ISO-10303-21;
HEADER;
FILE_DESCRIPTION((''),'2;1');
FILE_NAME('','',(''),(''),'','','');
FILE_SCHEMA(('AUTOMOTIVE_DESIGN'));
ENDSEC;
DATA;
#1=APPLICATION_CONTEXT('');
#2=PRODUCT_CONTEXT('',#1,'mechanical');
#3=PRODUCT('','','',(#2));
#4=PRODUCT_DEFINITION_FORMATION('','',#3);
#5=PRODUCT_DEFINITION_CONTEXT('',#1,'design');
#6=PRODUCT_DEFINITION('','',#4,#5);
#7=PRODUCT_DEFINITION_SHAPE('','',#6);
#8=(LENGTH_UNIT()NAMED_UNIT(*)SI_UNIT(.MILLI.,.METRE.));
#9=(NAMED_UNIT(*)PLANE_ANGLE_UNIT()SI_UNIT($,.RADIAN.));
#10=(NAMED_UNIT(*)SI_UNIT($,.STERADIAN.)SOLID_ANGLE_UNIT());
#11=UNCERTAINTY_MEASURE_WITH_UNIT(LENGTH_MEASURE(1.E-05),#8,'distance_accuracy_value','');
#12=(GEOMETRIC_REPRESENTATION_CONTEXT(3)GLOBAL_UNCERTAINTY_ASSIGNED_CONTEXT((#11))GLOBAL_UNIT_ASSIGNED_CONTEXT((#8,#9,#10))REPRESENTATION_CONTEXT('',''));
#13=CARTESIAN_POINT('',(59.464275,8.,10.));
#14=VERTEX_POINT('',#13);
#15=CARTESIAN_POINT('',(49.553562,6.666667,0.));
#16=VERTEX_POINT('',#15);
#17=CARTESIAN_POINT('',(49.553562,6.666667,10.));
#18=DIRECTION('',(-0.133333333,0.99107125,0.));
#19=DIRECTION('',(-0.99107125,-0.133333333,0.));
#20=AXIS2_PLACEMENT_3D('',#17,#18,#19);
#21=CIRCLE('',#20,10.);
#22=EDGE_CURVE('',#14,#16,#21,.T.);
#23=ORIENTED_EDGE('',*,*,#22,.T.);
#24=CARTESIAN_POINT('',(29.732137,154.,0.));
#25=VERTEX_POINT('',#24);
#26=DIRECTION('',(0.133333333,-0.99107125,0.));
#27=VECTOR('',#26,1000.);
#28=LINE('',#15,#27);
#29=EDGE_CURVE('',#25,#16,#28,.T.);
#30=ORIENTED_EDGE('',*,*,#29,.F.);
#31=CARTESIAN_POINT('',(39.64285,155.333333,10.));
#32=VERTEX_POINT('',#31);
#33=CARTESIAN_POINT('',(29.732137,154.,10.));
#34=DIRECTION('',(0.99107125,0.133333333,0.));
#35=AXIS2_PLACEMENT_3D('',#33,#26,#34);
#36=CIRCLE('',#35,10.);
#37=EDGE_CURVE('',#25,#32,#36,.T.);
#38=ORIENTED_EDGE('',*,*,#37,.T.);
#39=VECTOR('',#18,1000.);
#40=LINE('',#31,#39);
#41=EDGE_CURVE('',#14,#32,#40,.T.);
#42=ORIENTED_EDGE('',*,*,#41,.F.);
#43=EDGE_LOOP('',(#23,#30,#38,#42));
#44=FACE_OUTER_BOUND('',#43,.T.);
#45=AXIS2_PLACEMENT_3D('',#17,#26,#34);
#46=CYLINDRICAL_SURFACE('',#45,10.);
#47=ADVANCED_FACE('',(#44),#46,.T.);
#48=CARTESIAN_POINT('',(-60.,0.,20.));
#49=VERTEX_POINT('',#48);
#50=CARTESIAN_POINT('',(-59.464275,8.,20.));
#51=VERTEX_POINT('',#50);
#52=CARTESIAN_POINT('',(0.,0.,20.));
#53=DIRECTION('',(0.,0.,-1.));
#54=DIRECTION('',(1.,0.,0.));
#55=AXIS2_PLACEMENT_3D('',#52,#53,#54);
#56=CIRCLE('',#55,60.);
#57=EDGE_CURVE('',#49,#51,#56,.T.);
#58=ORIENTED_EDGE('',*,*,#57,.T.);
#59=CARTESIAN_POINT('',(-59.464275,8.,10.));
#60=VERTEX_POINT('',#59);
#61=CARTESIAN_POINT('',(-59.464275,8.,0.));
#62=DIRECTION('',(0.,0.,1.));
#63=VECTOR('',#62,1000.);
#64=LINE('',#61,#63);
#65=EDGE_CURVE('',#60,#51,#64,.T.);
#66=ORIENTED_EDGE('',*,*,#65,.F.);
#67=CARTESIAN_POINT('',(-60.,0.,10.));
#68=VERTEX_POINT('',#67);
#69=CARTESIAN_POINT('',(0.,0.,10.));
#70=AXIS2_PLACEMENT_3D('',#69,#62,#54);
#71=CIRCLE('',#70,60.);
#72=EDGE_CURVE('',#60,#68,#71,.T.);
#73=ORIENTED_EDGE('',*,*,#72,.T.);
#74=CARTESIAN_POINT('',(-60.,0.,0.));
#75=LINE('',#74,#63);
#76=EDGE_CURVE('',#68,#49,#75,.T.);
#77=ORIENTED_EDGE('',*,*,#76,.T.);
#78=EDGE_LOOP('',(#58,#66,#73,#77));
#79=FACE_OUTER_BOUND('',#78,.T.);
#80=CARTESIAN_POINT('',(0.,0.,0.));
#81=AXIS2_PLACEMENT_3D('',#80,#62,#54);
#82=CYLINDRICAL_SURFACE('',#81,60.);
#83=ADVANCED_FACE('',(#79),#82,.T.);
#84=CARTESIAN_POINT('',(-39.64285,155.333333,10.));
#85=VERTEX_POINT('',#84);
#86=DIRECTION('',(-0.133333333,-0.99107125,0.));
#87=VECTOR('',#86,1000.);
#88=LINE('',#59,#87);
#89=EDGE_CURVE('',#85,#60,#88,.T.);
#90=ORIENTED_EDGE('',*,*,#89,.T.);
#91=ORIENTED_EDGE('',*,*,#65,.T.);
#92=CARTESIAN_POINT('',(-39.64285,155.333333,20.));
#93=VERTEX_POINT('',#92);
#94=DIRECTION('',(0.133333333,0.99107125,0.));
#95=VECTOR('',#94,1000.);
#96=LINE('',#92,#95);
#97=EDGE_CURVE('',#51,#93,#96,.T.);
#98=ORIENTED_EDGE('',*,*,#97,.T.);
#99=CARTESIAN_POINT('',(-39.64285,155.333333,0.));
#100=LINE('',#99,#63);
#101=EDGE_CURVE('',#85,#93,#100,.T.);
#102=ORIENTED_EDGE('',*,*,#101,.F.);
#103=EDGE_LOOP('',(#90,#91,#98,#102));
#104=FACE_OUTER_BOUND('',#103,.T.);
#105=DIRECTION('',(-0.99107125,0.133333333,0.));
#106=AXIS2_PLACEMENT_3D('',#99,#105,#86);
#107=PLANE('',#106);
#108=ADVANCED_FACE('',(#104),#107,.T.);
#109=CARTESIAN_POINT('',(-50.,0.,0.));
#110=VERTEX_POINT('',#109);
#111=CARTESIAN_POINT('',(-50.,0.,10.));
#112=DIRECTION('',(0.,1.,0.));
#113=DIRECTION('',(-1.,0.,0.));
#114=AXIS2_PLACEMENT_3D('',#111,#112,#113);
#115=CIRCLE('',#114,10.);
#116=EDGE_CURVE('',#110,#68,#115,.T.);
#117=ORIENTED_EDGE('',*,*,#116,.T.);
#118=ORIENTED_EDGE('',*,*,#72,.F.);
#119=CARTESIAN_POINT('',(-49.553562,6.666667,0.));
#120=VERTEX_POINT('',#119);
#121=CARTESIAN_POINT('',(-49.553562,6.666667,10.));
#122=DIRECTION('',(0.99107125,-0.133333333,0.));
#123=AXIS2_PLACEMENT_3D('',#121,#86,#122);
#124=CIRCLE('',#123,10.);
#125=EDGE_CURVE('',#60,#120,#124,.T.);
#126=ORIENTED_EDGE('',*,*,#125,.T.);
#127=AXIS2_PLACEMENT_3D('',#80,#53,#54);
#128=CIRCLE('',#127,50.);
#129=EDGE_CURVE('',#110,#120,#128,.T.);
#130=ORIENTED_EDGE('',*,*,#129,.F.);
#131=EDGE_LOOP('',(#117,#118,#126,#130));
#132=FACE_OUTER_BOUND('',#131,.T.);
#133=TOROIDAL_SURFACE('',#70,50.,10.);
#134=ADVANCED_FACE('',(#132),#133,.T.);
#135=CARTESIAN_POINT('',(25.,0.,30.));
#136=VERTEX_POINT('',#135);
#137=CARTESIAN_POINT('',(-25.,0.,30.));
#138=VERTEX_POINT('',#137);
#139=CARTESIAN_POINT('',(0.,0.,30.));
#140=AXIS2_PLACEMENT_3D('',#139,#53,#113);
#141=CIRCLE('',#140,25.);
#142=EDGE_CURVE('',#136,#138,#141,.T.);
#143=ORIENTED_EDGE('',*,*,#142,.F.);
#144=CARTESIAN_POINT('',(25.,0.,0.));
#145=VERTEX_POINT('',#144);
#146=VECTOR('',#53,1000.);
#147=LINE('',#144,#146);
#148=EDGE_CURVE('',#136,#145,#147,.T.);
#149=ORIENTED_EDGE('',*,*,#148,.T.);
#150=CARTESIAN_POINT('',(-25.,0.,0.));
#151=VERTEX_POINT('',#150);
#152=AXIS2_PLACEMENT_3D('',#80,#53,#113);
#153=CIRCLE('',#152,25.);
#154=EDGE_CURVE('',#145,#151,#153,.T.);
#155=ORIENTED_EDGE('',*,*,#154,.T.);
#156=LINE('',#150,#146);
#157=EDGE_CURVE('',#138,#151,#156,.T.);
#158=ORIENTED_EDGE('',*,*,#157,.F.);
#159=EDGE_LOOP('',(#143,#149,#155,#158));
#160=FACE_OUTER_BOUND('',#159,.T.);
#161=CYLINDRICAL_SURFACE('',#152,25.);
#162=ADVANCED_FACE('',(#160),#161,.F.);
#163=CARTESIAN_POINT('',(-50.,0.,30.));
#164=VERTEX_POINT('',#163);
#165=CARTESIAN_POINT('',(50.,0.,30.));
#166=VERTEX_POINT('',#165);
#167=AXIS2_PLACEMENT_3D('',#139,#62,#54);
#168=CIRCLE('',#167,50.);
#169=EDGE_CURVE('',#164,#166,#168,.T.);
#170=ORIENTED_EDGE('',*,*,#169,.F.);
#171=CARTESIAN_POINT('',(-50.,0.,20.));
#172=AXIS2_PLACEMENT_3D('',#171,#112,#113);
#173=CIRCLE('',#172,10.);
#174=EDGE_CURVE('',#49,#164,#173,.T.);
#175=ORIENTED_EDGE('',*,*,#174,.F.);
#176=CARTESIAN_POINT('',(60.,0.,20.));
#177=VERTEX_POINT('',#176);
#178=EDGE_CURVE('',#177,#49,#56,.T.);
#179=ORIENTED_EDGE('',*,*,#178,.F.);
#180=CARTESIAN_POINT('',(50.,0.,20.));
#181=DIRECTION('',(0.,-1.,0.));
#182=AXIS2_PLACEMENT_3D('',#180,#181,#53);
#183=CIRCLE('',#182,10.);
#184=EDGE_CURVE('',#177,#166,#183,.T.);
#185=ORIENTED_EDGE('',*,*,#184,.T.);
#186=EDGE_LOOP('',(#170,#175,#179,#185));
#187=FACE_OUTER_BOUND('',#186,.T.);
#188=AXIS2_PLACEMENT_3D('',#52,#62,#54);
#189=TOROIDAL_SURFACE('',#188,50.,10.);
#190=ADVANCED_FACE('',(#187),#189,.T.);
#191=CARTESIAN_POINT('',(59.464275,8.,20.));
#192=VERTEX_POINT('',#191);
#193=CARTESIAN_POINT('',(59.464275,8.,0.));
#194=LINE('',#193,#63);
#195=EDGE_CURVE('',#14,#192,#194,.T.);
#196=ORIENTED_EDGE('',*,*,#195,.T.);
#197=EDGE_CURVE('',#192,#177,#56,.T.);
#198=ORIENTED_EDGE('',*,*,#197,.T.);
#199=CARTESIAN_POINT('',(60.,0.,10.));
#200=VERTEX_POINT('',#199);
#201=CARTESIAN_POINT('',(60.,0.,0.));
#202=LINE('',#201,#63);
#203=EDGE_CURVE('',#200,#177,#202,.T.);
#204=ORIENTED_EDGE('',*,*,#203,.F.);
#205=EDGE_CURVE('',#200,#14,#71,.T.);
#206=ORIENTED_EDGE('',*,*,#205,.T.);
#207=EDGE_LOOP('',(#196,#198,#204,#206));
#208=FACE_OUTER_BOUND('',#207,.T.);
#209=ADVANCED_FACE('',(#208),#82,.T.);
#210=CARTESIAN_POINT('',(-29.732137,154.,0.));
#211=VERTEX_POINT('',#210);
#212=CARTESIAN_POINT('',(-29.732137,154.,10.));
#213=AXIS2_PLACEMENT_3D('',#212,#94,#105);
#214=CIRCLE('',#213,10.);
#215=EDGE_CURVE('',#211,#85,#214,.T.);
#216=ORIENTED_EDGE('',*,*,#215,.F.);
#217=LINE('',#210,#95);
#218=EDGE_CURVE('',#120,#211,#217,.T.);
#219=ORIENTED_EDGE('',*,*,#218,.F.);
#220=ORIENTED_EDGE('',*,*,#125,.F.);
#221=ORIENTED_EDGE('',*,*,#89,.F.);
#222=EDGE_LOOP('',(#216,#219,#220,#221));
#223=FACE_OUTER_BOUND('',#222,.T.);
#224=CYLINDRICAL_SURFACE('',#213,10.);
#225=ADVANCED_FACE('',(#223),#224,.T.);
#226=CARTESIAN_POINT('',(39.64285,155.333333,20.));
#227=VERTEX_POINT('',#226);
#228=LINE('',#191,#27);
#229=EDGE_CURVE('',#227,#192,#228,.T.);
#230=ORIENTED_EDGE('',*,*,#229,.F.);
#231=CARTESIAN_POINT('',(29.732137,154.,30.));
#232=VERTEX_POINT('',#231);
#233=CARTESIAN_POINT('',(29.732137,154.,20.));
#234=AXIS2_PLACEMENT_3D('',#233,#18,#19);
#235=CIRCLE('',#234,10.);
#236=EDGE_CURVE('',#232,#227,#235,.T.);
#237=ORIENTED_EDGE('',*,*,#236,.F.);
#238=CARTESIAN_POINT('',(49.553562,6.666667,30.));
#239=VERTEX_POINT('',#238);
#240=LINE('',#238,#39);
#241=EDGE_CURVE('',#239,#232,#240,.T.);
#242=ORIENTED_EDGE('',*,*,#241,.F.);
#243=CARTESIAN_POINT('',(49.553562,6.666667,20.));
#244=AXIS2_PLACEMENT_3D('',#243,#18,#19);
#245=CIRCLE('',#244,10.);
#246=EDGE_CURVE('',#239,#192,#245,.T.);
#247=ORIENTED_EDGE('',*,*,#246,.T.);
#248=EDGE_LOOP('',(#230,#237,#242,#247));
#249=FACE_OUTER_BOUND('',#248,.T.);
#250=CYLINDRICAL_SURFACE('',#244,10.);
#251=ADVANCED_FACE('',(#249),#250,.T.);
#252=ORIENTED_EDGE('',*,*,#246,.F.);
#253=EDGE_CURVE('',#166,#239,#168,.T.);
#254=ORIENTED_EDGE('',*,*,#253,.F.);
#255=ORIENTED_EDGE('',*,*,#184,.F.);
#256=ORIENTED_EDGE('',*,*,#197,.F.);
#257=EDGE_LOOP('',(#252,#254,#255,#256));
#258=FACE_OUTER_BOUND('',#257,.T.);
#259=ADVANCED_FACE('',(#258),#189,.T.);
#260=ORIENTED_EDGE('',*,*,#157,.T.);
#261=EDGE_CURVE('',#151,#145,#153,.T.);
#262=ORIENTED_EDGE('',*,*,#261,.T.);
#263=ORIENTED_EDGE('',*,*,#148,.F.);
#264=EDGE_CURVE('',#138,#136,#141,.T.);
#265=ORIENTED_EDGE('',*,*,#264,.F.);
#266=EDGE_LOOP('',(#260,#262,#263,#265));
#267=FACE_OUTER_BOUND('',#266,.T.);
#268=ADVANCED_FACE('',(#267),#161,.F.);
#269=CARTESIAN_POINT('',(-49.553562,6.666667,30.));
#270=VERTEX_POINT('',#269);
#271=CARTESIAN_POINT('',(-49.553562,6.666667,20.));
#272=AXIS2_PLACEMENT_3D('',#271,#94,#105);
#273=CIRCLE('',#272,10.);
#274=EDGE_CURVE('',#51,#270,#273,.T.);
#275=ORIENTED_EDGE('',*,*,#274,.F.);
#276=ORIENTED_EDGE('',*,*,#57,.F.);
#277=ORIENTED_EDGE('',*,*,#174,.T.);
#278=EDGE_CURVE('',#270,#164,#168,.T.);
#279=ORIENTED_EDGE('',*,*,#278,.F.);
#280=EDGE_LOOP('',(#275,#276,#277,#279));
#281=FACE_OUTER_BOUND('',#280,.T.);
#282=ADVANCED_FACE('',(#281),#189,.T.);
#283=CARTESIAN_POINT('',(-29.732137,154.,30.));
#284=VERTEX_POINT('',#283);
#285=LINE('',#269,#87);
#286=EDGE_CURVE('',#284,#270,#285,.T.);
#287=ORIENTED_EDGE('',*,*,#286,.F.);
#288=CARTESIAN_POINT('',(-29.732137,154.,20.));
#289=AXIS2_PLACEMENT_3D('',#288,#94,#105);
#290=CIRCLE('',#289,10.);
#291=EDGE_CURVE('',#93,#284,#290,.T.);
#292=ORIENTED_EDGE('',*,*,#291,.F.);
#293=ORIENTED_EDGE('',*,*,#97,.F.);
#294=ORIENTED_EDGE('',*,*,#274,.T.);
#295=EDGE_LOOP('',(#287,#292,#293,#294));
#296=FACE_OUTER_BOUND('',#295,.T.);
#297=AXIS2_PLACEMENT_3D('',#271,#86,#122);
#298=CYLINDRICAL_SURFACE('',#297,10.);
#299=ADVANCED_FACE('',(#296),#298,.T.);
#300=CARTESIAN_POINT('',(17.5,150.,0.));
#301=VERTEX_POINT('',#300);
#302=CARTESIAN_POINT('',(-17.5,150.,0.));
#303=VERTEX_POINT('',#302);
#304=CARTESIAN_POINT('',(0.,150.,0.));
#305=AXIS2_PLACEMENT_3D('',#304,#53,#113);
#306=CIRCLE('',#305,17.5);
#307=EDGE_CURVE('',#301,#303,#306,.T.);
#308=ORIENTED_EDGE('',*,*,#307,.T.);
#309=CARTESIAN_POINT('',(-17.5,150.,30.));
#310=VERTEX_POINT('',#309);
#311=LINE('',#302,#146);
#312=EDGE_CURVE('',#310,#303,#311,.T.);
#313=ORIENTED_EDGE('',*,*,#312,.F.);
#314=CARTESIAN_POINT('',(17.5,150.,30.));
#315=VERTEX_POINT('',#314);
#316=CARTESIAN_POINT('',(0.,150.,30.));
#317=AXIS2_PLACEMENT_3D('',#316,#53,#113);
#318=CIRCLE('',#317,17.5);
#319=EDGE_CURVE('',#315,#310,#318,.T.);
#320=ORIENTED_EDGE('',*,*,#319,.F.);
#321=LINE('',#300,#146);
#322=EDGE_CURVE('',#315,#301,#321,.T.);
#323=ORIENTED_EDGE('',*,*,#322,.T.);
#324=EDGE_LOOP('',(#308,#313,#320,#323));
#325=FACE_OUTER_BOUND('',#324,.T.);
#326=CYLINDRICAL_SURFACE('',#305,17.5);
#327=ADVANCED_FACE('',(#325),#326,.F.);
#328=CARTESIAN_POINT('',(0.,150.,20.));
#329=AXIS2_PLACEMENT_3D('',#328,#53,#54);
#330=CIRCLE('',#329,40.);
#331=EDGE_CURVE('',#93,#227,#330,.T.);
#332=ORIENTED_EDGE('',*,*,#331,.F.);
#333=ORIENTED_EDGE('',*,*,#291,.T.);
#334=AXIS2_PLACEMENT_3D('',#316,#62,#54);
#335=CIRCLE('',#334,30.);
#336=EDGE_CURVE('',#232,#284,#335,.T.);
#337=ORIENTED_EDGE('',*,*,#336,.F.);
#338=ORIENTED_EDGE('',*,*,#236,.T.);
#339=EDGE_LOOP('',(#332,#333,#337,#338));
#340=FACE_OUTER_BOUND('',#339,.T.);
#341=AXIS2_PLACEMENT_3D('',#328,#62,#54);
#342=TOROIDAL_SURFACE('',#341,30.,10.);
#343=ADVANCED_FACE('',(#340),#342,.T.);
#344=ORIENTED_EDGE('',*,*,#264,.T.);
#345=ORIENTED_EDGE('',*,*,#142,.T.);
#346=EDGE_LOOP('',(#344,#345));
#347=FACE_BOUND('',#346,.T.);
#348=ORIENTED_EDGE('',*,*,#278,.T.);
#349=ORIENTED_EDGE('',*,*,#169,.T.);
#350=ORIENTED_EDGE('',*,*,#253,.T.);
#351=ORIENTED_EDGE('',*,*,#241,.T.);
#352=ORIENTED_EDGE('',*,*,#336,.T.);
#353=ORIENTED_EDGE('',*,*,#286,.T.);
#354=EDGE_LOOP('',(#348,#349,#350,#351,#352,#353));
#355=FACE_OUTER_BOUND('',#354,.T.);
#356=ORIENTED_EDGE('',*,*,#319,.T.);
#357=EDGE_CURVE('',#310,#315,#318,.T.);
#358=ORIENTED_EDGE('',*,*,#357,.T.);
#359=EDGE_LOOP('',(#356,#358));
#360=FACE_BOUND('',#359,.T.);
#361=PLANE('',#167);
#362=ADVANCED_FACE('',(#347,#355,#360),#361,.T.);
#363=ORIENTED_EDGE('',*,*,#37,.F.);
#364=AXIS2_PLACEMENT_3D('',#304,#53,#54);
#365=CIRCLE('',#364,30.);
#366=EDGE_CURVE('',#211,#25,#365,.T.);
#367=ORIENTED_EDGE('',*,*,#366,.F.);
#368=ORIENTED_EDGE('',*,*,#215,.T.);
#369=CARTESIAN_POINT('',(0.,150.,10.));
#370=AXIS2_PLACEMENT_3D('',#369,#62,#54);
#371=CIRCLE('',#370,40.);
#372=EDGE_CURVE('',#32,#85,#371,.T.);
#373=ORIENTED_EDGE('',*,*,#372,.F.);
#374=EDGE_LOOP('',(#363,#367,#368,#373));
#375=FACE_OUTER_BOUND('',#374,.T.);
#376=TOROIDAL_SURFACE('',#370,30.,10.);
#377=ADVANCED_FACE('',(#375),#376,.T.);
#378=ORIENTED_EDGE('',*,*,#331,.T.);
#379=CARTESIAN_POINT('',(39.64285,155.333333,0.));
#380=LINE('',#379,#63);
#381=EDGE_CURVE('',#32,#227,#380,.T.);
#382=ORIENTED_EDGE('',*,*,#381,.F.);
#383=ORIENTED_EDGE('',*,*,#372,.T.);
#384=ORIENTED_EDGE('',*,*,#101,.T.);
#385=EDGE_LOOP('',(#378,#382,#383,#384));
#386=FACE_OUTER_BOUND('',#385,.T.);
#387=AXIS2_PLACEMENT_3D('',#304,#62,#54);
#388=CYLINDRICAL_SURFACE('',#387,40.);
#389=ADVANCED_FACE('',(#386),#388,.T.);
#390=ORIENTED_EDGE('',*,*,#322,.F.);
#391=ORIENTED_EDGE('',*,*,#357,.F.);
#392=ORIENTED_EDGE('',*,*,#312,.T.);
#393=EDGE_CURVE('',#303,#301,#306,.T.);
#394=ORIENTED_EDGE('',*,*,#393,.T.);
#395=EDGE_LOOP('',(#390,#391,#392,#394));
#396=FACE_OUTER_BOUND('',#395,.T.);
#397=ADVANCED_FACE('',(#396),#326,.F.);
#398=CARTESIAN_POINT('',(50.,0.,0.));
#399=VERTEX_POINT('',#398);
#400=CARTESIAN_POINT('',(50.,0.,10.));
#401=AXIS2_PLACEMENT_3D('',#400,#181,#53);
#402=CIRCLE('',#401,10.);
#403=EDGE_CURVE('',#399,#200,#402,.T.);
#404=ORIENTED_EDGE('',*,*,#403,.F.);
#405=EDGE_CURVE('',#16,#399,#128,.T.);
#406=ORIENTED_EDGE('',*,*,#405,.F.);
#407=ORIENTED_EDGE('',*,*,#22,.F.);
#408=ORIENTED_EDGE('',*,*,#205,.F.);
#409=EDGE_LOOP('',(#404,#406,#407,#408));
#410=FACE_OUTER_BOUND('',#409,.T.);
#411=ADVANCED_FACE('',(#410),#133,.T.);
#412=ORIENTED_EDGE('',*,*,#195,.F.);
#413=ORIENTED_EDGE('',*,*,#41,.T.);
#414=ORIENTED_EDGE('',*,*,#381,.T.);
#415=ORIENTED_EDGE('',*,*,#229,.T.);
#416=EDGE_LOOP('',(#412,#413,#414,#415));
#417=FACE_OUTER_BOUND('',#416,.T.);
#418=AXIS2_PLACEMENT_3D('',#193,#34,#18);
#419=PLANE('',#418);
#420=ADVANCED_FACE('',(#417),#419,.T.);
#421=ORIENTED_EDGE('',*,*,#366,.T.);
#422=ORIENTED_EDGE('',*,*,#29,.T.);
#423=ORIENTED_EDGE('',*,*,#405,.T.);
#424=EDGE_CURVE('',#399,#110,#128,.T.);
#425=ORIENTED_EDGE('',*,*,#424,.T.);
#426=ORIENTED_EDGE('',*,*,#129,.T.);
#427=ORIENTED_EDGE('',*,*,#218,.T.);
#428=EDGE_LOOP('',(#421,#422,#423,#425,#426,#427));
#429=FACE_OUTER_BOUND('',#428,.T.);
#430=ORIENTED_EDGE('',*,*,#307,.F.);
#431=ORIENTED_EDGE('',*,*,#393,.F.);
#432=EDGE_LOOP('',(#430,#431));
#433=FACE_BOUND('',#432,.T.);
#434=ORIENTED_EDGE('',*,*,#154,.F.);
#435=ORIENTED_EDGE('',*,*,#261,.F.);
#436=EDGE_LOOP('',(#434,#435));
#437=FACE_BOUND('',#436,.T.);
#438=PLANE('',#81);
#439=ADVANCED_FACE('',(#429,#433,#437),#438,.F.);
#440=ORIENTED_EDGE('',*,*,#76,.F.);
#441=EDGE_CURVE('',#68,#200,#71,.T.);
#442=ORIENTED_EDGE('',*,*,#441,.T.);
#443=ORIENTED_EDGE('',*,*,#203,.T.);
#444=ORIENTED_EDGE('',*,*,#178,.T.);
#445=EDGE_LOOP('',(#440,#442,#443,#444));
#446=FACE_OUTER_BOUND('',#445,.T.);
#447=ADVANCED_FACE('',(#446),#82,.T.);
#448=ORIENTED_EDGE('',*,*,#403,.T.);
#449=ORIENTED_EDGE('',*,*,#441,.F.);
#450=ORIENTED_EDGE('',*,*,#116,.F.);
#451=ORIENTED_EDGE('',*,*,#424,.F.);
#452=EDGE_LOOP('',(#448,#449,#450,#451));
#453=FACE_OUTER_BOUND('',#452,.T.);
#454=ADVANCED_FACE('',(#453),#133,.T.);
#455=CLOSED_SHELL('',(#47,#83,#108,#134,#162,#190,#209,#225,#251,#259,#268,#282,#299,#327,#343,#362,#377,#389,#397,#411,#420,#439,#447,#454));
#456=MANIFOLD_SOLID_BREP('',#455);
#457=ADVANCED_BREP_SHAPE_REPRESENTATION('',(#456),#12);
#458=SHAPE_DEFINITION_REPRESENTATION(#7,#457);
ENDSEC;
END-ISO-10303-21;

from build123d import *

# Parameters (mm, degrees)
BOSS_EXTRUDE1_DEPTH   = 30
M30_CLEARANCE_HOLE1_D = 35
M45_CLEARANCE_HOLE1_D = 50
FILLET1_R             = 10


with BuildPart() as part:
    # Sketch1 → Boss-Extrude1 (new body)
    with BuildSketch(Plane.XY.offset(30)):
        with BuildLine():
            Line((59.464274989, 8), (39.642849993, 155.333333333))
            ThreePointArc((39.642849993, 155.333333333), (0, 190), (-39.642849993, 155.333333333))
            Line((-39.642849993, 155.333333333), (-59.464274989, 8))
            ThreePointArc((-59.464274989, 8), (0, -60), (59.464274989, 8))
        make_face()
    extrude(amount=-BOSS_EXTRUDE1_DEPTH)

    # M30 Clearance Hole1 (through all)
    with Locations(Plane(origin=(0, 0, 0), x_dir=(-1, 0, 0), z_dir=(0, 0, -1))):
        with Locations((0, 150)):
            Hole(M30_CLEARANCE_HOLE1_D / 2)

    # M45 Clearance Hole1 (through all)
    with Locations(Plane(origin=(0, 0, 0), x_dir=(-1, 0, 0), z_dir=(0, 0, -1))):
        with Locations((0, 0)):
            Hole(M45_CLEARANCE_HOLE1_D / 2)

    # Fillet1
    fillet1_edges = [part.edges().sort_by_distance(p)[0] for p in [
        (0, 190, 0),
        (-49.553562491, 81.666666667, 0),
        (0, -60, 0),
        (-49.553562491, 81.666666667, 30),
        (0, 190, 30),
        (49.553562491, 81.666666667, 30),
        (0, -60, 30),
        (49.553562491, 81.666666667, 0),
    ]]
    fillet(fillet1_edges, radius=FILLET1_R)


solid = part.part
